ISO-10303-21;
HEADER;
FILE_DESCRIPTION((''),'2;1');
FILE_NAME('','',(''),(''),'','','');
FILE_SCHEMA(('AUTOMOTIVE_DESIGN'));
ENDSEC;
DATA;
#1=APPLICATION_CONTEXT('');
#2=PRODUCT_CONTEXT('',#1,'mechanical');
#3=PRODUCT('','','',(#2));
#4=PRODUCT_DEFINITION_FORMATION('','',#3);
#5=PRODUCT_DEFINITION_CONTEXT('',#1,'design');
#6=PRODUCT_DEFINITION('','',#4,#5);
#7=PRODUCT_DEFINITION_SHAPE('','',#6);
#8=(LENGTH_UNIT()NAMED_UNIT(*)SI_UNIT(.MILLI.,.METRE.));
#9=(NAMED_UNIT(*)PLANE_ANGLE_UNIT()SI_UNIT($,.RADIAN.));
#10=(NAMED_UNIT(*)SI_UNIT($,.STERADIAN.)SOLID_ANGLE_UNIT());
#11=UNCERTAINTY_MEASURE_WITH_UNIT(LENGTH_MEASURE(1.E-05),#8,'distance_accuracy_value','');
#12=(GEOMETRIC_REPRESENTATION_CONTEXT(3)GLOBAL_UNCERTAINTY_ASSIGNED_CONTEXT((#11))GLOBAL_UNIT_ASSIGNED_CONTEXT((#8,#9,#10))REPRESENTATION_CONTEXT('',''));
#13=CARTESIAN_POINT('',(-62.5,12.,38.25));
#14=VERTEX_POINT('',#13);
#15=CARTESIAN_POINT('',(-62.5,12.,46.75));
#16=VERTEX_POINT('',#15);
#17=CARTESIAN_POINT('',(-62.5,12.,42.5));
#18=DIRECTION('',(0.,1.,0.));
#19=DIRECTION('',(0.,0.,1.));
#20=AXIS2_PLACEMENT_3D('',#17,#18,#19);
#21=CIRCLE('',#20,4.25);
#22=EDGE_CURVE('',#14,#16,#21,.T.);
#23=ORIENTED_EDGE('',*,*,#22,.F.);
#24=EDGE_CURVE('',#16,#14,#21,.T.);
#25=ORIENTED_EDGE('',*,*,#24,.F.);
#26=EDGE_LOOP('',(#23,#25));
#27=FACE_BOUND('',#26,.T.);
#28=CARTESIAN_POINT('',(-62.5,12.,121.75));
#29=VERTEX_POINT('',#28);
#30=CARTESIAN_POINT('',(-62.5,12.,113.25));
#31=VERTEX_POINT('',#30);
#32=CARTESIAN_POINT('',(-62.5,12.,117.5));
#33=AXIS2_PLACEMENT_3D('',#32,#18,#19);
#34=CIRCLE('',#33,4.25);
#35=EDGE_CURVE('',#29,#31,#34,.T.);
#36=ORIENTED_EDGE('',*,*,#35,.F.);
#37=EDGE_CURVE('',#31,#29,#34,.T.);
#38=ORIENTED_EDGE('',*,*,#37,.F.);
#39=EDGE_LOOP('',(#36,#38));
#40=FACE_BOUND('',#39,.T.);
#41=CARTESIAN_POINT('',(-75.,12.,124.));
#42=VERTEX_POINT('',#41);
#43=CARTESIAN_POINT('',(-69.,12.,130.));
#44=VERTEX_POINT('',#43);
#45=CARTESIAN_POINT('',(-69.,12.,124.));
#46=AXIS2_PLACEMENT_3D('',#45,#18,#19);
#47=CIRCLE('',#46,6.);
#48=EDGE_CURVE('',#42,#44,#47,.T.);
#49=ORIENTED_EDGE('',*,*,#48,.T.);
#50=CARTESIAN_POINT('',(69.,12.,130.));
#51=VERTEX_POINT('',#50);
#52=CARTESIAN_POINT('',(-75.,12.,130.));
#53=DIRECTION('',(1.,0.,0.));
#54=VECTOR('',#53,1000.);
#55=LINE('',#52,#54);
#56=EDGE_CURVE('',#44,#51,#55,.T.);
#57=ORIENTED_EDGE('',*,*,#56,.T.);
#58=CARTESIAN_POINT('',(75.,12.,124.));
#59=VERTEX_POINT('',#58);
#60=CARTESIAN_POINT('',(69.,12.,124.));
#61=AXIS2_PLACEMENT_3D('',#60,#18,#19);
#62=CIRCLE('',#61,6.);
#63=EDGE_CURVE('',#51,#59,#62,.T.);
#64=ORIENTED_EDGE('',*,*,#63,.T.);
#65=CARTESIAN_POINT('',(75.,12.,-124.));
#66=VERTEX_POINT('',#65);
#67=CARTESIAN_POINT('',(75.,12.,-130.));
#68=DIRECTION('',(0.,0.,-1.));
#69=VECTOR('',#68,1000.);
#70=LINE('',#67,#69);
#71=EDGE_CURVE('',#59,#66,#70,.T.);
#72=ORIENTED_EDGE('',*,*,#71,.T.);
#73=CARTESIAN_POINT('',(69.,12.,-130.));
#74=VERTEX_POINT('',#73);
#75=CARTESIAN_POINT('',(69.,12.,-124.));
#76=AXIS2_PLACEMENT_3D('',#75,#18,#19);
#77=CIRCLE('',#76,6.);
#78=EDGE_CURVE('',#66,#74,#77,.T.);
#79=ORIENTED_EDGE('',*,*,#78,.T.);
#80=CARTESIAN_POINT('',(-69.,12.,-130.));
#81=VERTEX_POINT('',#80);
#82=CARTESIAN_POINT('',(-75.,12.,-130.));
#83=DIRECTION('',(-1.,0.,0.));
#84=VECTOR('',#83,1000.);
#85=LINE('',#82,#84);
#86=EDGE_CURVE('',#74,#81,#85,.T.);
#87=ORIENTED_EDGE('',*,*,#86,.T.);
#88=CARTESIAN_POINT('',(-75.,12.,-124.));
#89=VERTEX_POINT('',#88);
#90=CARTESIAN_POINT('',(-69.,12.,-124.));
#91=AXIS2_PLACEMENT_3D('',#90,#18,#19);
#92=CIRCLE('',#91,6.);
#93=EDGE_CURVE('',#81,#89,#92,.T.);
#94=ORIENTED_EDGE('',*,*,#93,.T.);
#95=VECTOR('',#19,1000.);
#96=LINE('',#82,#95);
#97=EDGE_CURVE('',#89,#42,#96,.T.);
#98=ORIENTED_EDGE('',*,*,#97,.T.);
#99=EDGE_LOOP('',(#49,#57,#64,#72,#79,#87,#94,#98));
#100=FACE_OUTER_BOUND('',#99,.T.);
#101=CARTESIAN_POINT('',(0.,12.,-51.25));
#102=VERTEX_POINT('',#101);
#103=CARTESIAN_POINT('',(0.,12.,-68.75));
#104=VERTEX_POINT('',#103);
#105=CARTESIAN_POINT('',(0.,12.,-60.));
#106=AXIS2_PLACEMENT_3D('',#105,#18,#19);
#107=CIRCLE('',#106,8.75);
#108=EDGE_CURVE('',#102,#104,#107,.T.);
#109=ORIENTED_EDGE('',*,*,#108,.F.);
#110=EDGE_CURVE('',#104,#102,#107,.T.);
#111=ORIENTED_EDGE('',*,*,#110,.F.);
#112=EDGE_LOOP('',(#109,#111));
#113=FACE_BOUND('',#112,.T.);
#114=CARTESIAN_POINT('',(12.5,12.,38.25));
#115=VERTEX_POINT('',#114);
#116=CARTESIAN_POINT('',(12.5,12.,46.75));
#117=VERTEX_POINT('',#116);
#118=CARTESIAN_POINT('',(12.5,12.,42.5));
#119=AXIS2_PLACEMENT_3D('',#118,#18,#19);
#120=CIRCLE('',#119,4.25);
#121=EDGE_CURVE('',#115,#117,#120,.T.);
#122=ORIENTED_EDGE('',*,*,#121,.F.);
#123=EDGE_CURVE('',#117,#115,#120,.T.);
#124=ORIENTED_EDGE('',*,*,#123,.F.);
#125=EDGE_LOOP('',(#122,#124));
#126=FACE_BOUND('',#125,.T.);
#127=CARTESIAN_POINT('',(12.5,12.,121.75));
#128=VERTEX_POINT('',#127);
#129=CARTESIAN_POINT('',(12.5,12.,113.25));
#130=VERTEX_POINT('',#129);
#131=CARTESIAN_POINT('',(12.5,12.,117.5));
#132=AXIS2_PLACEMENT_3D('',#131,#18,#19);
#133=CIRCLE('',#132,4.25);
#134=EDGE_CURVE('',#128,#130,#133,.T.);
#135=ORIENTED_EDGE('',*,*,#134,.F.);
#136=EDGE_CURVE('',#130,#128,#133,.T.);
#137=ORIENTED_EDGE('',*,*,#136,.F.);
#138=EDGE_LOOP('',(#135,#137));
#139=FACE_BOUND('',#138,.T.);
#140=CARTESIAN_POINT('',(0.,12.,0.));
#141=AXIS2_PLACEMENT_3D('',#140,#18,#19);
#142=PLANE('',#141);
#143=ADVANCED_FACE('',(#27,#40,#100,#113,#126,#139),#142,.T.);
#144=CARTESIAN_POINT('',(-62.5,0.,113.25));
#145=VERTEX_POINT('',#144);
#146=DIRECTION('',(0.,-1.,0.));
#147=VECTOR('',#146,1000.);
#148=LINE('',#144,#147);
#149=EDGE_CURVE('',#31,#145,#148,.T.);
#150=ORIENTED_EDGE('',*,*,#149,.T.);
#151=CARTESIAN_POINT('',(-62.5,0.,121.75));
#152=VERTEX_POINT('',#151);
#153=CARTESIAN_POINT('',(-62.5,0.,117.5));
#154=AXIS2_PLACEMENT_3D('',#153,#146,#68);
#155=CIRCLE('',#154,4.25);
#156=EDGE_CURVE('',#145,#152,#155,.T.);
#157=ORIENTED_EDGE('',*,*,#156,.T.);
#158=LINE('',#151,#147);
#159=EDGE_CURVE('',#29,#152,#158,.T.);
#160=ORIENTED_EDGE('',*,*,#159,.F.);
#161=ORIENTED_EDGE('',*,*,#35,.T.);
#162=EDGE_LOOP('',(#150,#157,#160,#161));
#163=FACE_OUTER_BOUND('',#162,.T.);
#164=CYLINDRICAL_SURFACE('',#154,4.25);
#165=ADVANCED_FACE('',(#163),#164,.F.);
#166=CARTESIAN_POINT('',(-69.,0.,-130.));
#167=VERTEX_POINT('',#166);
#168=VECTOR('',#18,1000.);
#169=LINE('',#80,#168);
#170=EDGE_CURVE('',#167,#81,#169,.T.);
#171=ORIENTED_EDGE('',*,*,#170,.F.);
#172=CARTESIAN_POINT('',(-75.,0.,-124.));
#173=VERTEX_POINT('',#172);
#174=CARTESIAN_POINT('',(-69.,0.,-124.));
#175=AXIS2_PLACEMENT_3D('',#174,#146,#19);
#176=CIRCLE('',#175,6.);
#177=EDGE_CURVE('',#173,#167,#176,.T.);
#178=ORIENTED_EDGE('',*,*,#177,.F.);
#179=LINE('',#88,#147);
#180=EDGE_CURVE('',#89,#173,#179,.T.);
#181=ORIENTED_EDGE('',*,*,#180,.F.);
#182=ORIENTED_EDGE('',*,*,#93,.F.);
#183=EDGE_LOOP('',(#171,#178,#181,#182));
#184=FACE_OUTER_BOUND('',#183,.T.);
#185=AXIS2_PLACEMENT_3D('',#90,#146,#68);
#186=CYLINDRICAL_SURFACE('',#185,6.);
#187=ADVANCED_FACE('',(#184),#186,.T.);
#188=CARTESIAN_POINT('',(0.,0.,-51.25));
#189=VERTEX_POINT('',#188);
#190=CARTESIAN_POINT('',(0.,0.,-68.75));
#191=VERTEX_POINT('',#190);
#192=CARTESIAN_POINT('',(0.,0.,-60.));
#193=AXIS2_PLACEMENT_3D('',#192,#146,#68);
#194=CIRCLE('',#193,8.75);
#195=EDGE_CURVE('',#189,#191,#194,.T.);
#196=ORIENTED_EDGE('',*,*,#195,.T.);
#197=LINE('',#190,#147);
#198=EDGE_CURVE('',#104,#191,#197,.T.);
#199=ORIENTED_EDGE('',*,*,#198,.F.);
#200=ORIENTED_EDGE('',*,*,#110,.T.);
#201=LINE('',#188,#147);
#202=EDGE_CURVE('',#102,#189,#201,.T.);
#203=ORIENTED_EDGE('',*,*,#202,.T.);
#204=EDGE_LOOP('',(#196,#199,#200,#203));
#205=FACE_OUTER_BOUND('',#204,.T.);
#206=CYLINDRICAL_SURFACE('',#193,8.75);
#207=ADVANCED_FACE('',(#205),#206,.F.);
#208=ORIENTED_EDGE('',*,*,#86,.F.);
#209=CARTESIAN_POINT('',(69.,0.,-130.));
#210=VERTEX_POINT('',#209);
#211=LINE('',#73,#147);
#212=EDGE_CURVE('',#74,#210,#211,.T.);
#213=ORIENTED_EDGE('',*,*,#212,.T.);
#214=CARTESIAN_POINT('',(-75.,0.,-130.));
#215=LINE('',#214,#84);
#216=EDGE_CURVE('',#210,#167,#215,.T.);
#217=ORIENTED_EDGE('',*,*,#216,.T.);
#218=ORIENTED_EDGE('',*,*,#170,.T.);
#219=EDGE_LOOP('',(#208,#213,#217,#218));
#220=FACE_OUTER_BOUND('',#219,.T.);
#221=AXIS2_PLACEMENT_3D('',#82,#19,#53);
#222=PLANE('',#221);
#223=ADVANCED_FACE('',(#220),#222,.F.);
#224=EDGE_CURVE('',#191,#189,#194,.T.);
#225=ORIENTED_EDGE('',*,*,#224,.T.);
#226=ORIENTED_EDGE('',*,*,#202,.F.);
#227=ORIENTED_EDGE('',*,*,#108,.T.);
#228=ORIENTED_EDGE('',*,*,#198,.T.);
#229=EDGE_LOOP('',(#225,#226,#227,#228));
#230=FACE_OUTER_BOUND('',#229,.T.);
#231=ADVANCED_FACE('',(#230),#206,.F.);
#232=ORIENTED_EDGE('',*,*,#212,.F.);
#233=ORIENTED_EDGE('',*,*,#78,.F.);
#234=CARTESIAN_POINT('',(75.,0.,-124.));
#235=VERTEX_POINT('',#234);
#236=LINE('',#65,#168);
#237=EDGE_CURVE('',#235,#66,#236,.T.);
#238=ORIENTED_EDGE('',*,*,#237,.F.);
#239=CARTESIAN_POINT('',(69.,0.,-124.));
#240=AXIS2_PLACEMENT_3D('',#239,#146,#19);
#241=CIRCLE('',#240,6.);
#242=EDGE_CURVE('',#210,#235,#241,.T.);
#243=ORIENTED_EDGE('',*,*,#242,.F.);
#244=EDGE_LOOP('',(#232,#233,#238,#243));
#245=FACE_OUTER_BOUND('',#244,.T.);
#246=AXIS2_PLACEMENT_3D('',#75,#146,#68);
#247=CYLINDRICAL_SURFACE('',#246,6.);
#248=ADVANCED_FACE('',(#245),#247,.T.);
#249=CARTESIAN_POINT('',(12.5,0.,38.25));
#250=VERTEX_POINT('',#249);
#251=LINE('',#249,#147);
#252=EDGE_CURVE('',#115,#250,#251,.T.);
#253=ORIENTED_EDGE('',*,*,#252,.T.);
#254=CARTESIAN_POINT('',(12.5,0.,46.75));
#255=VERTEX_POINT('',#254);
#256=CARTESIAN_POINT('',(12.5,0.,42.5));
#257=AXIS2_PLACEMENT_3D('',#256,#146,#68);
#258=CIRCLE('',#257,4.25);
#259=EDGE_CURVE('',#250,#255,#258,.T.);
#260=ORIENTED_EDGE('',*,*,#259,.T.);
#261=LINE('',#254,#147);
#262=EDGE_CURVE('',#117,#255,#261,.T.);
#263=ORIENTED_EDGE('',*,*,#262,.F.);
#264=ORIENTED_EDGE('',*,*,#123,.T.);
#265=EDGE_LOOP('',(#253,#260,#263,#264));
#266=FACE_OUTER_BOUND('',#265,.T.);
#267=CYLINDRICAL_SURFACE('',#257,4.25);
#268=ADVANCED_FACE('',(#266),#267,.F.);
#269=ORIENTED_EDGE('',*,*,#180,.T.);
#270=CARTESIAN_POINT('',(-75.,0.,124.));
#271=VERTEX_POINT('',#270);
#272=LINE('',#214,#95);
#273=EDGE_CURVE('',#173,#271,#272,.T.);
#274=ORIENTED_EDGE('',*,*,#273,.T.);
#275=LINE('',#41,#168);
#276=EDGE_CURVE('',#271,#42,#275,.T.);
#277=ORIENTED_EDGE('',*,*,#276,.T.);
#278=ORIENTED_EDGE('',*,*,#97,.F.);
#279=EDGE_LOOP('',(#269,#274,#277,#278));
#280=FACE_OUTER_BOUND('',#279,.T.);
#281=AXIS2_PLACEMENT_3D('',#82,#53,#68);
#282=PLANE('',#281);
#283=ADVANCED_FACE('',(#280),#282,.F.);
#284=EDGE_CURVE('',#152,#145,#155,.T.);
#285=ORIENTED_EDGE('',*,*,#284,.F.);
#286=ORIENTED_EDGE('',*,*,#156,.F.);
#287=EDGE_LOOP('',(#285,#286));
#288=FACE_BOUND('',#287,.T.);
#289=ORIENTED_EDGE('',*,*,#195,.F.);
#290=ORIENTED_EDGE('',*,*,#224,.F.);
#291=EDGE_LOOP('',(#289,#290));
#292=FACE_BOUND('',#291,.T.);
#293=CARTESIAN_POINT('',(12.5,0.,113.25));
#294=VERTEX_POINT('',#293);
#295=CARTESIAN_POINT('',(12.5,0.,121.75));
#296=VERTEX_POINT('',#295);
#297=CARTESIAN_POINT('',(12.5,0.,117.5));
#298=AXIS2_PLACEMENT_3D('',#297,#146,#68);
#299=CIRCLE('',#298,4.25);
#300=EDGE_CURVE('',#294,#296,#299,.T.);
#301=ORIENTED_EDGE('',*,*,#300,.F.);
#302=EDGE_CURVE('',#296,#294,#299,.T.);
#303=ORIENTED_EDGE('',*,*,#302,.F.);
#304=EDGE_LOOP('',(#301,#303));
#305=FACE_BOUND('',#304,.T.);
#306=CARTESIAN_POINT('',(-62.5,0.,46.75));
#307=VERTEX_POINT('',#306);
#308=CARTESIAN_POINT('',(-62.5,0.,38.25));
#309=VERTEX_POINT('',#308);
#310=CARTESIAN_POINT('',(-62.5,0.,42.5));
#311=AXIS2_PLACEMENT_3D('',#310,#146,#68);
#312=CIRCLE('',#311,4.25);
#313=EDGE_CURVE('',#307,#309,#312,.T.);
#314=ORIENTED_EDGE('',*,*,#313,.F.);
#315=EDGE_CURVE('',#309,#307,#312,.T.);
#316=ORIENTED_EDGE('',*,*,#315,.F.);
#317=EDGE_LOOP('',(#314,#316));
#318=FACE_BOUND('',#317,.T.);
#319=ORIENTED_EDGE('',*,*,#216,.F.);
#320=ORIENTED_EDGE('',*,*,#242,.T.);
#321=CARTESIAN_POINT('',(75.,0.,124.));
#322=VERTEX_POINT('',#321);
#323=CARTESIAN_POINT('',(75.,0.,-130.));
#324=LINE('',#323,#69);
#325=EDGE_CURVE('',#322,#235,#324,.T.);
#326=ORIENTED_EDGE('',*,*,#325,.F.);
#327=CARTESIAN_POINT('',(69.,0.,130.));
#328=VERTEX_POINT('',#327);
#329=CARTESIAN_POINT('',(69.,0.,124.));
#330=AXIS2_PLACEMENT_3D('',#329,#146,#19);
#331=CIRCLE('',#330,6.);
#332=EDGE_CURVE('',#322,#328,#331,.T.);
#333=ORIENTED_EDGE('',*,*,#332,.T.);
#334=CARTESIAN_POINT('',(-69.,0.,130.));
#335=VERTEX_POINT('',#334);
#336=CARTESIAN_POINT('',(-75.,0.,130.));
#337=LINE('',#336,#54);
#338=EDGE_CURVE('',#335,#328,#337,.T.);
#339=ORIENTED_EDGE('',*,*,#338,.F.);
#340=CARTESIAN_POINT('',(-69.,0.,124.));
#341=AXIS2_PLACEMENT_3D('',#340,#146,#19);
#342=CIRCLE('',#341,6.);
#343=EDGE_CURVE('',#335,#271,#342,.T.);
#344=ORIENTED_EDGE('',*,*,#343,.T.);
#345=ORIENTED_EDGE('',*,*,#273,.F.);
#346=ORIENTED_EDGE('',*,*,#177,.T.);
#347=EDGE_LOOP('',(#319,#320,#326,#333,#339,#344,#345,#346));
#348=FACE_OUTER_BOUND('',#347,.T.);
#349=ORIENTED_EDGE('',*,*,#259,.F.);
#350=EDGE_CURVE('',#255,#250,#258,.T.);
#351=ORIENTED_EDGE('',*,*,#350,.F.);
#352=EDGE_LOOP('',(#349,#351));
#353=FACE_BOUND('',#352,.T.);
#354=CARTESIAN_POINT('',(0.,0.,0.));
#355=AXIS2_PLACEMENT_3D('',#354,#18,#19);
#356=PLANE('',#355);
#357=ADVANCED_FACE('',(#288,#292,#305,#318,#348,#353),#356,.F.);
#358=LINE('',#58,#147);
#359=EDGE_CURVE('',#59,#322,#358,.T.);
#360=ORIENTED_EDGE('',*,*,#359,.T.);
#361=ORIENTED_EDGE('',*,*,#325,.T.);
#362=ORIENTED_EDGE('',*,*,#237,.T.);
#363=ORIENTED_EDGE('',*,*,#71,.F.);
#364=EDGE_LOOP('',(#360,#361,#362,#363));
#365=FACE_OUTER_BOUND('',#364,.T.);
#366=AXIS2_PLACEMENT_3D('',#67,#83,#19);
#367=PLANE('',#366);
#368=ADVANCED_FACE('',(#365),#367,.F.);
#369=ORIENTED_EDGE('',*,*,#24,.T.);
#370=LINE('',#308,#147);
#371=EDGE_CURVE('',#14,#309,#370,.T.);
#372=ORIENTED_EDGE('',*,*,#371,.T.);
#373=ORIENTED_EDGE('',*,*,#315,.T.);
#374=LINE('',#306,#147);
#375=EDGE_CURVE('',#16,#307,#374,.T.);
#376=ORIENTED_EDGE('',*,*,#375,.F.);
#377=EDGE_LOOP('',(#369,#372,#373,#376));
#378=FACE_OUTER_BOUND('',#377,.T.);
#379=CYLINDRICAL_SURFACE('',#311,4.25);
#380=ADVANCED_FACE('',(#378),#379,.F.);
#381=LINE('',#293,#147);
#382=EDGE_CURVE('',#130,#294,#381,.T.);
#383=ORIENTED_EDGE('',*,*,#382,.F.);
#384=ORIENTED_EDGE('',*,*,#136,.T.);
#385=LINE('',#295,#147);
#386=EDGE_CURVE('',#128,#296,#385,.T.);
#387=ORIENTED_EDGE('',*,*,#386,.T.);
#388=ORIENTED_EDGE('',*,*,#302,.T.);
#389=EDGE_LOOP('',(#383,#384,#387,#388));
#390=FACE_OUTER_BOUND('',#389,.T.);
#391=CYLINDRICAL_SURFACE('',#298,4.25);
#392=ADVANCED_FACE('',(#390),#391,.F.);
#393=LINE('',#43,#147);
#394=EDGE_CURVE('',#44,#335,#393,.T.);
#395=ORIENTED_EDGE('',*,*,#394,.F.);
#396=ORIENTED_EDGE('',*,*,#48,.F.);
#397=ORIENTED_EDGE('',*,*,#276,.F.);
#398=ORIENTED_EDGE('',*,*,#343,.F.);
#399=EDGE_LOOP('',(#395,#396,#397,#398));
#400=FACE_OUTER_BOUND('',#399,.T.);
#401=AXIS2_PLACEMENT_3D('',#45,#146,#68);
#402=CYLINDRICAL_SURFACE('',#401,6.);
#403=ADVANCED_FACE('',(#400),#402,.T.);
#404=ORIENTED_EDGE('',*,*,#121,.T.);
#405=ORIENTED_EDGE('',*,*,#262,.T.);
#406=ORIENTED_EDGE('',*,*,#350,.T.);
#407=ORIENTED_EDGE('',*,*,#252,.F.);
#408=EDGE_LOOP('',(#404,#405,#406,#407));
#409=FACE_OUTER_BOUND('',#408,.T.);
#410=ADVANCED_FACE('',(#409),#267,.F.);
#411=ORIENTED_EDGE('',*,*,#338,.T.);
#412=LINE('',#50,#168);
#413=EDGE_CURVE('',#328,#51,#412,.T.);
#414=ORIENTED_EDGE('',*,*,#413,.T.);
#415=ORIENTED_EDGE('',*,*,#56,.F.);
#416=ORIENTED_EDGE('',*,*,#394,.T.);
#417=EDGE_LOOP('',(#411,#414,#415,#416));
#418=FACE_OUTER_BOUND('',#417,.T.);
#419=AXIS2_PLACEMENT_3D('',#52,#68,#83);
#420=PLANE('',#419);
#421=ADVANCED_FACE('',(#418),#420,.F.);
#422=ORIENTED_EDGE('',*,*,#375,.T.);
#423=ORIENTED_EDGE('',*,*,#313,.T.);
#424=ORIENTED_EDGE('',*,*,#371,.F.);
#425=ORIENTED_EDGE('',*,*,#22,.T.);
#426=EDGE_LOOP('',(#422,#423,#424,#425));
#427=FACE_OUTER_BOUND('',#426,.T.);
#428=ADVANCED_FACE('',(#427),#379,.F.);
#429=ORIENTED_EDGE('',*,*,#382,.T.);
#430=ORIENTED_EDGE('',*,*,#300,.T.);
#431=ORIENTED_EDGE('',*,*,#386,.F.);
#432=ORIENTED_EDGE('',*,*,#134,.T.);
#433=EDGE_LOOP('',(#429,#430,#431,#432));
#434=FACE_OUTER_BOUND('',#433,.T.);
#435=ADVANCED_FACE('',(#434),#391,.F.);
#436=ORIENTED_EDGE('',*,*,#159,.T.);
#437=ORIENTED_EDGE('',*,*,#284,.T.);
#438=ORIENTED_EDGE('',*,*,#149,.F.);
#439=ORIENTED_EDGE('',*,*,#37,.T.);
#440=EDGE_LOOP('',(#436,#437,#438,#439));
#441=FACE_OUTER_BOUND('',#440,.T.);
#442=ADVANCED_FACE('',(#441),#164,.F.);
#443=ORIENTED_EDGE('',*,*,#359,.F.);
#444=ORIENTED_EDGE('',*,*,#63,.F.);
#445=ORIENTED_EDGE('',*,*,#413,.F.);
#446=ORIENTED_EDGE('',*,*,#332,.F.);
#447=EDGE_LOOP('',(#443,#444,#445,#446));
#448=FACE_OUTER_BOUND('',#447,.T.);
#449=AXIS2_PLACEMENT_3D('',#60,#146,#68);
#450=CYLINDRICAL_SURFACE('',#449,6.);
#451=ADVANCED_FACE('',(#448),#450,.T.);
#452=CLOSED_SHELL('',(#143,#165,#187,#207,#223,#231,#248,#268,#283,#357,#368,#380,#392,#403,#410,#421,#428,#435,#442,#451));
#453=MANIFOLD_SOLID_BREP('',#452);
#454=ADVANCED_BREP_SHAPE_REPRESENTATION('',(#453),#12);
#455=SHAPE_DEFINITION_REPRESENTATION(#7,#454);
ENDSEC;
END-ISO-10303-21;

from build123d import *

# Parameters (mm, degrees)
SKETCH_1_W              = 150
SKETCH_1_H              = 260
EXTRUDE_1_DEPTH         = 12
FILLET_1_R              = 6
HOLE_WIZARD_M20_1_D     = 17.5
HOLE_WIZARD_M20_1_DEPTH = 47.5
HOLE_WIZARD_M20_1_TIP   = 5.257530416
HOLE_WIZARD_M10_1_D     = 8.5
HOLE_WIZARD_M10_1_DEPTH = 24.5
HOLE_WIZARD_M10_1_TIP   = 2.553657631


with BuildPart() as part:
    # 草图1 → 凸台-拉伸1 (new body)
    with BuildSketch(Plane(origin=(0, 0, 0), x_dir=(1, 0, 0), z_dir=(0, 1, 0))):
        Rectangle(SKETCH_1_W, SKETCH_1_H)
    extrude(amount=EXTRUDE_1_DEPTH)

    # 圆角1
    fillet_1_edges = [part.edges().sort_by_distance(p)[0] for p in [
        (75, 6, 130),
        (-75, 6, 130),
        (-75, 6, -130),
        (75, 6, -130),
    ]]
    fillet(fillet_1_edges, radius=FILLET_1_R)

    # M20 螺纹孔1
    with Locations(Plane(origin=(0, 0, 0), x_dir=(-1, 0, 0), z_dir=(0, -1, 0))):
        with Locations((0, 60)):
            Hole(HOLE_WIZARD_M20_1_D / 2, depth=HOLE_WIZARD_M20_1_DEPTH)
            with Locations((0, 0, -(HOLE_WIZARD_M20_1_DEPTH + HOLE_WIZARD_M20_1_TIP / 2))):  # 118° drill point
                Cone(0, HOLE_WIZARD_M20_1_D / 2, HOLE_WIZARD_M20_1_TIP, mode=Mode.SUBTRACT)

    # M10 螺纹孔1
    with Locations(Plane(origin=(0, 0, 0), x_dir=(-1, 0, 0), z_dir=(0, -1, 0))):
        with Locations((62.5, -117.5), (62.5, -42.5), (-12.5, -42.5), (-12.5, -117.5)):
            Hole(HOLE_WIZARD_M10_1_D / 2, depth=HOLE_WIZARD_M10_1_DEPTH)
            with Locations((0, 0, -(HOLE_WIZARD_M10_1_DEPTH + HOLE_WIZARD_M10_1_TIP / 2))):  # 118° drill point
                Cone(0, HOLE_WIZARD_M10_1_D / 2, HOLE_WIZARD_M10_1_TIP, mode=Mode.SUBTRACT)


solid = part.part
